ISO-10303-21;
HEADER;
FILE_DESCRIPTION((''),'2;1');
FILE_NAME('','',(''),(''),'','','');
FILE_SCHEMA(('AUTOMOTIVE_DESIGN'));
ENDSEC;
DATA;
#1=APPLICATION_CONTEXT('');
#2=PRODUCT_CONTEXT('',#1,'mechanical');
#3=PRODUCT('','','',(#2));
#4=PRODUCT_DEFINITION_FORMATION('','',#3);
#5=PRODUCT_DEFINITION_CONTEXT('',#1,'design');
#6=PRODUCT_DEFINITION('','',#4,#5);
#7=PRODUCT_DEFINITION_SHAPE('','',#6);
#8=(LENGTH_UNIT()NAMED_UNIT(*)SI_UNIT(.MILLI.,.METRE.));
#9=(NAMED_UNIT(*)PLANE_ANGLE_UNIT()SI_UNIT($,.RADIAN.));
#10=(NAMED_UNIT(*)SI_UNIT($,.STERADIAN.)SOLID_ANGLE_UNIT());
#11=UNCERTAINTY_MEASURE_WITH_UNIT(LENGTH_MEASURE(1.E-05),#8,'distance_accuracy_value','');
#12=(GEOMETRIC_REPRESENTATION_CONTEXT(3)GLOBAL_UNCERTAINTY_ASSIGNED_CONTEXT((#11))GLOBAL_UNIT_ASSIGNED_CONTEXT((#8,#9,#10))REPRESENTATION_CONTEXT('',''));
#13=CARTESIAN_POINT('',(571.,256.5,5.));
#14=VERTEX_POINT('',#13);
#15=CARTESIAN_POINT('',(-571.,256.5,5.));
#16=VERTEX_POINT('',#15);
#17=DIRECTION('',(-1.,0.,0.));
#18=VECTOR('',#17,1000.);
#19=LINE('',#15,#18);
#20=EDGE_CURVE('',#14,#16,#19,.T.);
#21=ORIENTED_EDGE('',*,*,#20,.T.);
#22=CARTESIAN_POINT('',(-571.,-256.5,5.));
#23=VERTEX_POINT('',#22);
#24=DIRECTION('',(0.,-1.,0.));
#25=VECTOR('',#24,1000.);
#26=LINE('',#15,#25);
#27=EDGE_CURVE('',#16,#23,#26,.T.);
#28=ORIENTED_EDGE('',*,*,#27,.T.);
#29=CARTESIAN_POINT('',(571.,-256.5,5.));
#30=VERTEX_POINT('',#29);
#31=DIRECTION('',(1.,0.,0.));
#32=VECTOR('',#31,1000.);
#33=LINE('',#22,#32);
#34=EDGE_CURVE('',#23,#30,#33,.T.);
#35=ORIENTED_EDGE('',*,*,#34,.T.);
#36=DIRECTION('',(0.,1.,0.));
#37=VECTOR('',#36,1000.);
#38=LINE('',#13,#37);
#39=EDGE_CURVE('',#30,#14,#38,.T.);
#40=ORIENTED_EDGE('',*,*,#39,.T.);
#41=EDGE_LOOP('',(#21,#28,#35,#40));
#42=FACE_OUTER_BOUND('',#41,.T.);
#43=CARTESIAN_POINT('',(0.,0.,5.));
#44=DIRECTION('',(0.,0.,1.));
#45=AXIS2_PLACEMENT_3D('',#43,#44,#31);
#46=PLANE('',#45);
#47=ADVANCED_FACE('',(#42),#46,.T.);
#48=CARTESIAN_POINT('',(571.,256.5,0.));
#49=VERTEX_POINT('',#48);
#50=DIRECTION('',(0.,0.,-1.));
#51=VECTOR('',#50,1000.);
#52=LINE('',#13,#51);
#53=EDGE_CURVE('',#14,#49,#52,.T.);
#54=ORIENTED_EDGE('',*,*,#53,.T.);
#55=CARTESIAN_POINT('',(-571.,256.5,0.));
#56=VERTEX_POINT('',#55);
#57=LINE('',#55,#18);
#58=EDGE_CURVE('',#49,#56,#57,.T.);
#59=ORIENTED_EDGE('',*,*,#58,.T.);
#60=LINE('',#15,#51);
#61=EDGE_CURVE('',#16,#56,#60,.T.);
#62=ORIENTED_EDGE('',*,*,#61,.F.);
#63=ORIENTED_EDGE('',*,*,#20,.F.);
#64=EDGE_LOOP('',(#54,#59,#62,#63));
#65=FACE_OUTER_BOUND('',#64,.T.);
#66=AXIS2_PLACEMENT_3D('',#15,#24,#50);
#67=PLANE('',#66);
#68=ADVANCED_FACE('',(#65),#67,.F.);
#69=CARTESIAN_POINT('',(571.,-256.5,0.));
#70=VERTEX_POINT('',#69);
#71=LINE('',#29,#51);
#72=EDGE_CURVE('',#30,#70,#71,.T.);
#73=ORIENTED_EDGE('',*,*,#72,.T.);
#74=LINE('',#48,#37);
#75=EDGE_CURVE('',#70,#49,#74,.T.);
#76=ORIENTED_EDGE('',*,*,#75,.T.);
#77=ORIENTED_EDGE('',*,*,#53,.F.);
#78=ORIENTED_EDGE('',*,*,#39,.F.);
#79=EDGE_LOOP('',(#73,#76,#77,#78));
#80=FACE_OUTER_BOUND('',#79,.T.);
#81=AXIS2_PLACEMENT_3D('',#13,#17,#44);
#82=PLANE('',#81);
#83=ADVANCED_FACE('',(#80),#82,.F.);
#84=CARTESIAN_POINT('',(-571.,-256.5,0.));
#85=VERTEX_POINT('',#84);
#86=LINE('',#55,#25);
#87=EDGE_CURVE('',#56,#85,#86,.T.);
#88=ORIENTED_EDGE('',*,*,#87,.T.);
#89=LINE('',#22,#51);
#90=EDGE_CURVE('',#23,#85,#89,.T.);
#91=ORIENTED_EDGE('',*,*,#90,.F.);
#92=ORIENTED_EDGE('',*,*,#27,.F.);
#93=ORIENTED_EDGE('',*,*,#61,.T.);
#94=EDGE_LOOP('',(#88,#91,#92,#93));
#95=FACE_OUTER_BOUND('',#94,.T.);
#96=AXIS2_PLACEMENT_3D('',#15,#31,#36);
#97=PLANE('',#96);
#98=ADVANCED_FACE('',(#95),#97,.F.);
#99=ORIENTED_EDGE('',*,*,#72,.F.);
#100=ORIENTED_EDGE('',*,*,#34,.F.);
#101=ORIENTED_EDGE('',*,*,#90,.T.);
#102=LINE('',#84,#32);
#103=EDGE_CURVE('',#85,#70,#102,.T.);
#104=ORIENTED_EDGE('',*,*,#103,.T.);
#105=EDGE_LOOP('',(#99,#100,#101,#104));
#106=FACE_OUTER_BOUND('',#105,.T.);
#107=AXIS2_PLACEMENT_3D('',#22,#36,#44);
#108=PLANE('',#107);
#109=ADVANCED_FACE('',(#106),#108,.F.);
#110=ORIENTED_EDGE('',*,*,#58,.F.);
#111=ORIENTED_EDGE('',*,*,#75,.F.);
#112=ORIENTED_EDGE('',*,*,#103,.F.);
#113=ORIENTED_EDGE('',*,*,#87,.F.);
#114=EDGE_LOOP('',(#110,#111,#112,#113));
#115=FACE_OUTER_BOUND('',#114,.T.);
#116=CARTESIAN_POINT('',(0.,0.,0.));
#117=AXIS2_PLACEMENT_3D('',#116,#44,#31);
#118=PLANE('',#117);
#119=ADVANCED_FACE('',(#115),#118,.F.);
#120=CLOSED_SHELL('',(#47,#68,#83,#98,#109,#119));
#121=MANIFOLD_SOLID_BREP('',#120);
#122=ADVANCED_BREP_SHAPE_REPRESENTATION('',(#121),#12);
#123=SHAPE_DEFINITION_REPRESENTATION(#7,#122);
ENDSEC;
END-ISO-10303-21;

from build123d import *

# Parameters (mm, degrees)
SKETCH_1_W      = 1142
SKETCH_1_H      = 513
EXTRUDE_1_DEPTH = 5


with BuildPart() as part:
    # 草图1 → 凸台-拉伸1 (new body)
    with BuildSketch(Plane.XY):
        Rectangle(SKETCH_1_W, SKETCH_1_H)
    extrude(amount=EXTRUDE_1_DEPTH)


solid = part.part
